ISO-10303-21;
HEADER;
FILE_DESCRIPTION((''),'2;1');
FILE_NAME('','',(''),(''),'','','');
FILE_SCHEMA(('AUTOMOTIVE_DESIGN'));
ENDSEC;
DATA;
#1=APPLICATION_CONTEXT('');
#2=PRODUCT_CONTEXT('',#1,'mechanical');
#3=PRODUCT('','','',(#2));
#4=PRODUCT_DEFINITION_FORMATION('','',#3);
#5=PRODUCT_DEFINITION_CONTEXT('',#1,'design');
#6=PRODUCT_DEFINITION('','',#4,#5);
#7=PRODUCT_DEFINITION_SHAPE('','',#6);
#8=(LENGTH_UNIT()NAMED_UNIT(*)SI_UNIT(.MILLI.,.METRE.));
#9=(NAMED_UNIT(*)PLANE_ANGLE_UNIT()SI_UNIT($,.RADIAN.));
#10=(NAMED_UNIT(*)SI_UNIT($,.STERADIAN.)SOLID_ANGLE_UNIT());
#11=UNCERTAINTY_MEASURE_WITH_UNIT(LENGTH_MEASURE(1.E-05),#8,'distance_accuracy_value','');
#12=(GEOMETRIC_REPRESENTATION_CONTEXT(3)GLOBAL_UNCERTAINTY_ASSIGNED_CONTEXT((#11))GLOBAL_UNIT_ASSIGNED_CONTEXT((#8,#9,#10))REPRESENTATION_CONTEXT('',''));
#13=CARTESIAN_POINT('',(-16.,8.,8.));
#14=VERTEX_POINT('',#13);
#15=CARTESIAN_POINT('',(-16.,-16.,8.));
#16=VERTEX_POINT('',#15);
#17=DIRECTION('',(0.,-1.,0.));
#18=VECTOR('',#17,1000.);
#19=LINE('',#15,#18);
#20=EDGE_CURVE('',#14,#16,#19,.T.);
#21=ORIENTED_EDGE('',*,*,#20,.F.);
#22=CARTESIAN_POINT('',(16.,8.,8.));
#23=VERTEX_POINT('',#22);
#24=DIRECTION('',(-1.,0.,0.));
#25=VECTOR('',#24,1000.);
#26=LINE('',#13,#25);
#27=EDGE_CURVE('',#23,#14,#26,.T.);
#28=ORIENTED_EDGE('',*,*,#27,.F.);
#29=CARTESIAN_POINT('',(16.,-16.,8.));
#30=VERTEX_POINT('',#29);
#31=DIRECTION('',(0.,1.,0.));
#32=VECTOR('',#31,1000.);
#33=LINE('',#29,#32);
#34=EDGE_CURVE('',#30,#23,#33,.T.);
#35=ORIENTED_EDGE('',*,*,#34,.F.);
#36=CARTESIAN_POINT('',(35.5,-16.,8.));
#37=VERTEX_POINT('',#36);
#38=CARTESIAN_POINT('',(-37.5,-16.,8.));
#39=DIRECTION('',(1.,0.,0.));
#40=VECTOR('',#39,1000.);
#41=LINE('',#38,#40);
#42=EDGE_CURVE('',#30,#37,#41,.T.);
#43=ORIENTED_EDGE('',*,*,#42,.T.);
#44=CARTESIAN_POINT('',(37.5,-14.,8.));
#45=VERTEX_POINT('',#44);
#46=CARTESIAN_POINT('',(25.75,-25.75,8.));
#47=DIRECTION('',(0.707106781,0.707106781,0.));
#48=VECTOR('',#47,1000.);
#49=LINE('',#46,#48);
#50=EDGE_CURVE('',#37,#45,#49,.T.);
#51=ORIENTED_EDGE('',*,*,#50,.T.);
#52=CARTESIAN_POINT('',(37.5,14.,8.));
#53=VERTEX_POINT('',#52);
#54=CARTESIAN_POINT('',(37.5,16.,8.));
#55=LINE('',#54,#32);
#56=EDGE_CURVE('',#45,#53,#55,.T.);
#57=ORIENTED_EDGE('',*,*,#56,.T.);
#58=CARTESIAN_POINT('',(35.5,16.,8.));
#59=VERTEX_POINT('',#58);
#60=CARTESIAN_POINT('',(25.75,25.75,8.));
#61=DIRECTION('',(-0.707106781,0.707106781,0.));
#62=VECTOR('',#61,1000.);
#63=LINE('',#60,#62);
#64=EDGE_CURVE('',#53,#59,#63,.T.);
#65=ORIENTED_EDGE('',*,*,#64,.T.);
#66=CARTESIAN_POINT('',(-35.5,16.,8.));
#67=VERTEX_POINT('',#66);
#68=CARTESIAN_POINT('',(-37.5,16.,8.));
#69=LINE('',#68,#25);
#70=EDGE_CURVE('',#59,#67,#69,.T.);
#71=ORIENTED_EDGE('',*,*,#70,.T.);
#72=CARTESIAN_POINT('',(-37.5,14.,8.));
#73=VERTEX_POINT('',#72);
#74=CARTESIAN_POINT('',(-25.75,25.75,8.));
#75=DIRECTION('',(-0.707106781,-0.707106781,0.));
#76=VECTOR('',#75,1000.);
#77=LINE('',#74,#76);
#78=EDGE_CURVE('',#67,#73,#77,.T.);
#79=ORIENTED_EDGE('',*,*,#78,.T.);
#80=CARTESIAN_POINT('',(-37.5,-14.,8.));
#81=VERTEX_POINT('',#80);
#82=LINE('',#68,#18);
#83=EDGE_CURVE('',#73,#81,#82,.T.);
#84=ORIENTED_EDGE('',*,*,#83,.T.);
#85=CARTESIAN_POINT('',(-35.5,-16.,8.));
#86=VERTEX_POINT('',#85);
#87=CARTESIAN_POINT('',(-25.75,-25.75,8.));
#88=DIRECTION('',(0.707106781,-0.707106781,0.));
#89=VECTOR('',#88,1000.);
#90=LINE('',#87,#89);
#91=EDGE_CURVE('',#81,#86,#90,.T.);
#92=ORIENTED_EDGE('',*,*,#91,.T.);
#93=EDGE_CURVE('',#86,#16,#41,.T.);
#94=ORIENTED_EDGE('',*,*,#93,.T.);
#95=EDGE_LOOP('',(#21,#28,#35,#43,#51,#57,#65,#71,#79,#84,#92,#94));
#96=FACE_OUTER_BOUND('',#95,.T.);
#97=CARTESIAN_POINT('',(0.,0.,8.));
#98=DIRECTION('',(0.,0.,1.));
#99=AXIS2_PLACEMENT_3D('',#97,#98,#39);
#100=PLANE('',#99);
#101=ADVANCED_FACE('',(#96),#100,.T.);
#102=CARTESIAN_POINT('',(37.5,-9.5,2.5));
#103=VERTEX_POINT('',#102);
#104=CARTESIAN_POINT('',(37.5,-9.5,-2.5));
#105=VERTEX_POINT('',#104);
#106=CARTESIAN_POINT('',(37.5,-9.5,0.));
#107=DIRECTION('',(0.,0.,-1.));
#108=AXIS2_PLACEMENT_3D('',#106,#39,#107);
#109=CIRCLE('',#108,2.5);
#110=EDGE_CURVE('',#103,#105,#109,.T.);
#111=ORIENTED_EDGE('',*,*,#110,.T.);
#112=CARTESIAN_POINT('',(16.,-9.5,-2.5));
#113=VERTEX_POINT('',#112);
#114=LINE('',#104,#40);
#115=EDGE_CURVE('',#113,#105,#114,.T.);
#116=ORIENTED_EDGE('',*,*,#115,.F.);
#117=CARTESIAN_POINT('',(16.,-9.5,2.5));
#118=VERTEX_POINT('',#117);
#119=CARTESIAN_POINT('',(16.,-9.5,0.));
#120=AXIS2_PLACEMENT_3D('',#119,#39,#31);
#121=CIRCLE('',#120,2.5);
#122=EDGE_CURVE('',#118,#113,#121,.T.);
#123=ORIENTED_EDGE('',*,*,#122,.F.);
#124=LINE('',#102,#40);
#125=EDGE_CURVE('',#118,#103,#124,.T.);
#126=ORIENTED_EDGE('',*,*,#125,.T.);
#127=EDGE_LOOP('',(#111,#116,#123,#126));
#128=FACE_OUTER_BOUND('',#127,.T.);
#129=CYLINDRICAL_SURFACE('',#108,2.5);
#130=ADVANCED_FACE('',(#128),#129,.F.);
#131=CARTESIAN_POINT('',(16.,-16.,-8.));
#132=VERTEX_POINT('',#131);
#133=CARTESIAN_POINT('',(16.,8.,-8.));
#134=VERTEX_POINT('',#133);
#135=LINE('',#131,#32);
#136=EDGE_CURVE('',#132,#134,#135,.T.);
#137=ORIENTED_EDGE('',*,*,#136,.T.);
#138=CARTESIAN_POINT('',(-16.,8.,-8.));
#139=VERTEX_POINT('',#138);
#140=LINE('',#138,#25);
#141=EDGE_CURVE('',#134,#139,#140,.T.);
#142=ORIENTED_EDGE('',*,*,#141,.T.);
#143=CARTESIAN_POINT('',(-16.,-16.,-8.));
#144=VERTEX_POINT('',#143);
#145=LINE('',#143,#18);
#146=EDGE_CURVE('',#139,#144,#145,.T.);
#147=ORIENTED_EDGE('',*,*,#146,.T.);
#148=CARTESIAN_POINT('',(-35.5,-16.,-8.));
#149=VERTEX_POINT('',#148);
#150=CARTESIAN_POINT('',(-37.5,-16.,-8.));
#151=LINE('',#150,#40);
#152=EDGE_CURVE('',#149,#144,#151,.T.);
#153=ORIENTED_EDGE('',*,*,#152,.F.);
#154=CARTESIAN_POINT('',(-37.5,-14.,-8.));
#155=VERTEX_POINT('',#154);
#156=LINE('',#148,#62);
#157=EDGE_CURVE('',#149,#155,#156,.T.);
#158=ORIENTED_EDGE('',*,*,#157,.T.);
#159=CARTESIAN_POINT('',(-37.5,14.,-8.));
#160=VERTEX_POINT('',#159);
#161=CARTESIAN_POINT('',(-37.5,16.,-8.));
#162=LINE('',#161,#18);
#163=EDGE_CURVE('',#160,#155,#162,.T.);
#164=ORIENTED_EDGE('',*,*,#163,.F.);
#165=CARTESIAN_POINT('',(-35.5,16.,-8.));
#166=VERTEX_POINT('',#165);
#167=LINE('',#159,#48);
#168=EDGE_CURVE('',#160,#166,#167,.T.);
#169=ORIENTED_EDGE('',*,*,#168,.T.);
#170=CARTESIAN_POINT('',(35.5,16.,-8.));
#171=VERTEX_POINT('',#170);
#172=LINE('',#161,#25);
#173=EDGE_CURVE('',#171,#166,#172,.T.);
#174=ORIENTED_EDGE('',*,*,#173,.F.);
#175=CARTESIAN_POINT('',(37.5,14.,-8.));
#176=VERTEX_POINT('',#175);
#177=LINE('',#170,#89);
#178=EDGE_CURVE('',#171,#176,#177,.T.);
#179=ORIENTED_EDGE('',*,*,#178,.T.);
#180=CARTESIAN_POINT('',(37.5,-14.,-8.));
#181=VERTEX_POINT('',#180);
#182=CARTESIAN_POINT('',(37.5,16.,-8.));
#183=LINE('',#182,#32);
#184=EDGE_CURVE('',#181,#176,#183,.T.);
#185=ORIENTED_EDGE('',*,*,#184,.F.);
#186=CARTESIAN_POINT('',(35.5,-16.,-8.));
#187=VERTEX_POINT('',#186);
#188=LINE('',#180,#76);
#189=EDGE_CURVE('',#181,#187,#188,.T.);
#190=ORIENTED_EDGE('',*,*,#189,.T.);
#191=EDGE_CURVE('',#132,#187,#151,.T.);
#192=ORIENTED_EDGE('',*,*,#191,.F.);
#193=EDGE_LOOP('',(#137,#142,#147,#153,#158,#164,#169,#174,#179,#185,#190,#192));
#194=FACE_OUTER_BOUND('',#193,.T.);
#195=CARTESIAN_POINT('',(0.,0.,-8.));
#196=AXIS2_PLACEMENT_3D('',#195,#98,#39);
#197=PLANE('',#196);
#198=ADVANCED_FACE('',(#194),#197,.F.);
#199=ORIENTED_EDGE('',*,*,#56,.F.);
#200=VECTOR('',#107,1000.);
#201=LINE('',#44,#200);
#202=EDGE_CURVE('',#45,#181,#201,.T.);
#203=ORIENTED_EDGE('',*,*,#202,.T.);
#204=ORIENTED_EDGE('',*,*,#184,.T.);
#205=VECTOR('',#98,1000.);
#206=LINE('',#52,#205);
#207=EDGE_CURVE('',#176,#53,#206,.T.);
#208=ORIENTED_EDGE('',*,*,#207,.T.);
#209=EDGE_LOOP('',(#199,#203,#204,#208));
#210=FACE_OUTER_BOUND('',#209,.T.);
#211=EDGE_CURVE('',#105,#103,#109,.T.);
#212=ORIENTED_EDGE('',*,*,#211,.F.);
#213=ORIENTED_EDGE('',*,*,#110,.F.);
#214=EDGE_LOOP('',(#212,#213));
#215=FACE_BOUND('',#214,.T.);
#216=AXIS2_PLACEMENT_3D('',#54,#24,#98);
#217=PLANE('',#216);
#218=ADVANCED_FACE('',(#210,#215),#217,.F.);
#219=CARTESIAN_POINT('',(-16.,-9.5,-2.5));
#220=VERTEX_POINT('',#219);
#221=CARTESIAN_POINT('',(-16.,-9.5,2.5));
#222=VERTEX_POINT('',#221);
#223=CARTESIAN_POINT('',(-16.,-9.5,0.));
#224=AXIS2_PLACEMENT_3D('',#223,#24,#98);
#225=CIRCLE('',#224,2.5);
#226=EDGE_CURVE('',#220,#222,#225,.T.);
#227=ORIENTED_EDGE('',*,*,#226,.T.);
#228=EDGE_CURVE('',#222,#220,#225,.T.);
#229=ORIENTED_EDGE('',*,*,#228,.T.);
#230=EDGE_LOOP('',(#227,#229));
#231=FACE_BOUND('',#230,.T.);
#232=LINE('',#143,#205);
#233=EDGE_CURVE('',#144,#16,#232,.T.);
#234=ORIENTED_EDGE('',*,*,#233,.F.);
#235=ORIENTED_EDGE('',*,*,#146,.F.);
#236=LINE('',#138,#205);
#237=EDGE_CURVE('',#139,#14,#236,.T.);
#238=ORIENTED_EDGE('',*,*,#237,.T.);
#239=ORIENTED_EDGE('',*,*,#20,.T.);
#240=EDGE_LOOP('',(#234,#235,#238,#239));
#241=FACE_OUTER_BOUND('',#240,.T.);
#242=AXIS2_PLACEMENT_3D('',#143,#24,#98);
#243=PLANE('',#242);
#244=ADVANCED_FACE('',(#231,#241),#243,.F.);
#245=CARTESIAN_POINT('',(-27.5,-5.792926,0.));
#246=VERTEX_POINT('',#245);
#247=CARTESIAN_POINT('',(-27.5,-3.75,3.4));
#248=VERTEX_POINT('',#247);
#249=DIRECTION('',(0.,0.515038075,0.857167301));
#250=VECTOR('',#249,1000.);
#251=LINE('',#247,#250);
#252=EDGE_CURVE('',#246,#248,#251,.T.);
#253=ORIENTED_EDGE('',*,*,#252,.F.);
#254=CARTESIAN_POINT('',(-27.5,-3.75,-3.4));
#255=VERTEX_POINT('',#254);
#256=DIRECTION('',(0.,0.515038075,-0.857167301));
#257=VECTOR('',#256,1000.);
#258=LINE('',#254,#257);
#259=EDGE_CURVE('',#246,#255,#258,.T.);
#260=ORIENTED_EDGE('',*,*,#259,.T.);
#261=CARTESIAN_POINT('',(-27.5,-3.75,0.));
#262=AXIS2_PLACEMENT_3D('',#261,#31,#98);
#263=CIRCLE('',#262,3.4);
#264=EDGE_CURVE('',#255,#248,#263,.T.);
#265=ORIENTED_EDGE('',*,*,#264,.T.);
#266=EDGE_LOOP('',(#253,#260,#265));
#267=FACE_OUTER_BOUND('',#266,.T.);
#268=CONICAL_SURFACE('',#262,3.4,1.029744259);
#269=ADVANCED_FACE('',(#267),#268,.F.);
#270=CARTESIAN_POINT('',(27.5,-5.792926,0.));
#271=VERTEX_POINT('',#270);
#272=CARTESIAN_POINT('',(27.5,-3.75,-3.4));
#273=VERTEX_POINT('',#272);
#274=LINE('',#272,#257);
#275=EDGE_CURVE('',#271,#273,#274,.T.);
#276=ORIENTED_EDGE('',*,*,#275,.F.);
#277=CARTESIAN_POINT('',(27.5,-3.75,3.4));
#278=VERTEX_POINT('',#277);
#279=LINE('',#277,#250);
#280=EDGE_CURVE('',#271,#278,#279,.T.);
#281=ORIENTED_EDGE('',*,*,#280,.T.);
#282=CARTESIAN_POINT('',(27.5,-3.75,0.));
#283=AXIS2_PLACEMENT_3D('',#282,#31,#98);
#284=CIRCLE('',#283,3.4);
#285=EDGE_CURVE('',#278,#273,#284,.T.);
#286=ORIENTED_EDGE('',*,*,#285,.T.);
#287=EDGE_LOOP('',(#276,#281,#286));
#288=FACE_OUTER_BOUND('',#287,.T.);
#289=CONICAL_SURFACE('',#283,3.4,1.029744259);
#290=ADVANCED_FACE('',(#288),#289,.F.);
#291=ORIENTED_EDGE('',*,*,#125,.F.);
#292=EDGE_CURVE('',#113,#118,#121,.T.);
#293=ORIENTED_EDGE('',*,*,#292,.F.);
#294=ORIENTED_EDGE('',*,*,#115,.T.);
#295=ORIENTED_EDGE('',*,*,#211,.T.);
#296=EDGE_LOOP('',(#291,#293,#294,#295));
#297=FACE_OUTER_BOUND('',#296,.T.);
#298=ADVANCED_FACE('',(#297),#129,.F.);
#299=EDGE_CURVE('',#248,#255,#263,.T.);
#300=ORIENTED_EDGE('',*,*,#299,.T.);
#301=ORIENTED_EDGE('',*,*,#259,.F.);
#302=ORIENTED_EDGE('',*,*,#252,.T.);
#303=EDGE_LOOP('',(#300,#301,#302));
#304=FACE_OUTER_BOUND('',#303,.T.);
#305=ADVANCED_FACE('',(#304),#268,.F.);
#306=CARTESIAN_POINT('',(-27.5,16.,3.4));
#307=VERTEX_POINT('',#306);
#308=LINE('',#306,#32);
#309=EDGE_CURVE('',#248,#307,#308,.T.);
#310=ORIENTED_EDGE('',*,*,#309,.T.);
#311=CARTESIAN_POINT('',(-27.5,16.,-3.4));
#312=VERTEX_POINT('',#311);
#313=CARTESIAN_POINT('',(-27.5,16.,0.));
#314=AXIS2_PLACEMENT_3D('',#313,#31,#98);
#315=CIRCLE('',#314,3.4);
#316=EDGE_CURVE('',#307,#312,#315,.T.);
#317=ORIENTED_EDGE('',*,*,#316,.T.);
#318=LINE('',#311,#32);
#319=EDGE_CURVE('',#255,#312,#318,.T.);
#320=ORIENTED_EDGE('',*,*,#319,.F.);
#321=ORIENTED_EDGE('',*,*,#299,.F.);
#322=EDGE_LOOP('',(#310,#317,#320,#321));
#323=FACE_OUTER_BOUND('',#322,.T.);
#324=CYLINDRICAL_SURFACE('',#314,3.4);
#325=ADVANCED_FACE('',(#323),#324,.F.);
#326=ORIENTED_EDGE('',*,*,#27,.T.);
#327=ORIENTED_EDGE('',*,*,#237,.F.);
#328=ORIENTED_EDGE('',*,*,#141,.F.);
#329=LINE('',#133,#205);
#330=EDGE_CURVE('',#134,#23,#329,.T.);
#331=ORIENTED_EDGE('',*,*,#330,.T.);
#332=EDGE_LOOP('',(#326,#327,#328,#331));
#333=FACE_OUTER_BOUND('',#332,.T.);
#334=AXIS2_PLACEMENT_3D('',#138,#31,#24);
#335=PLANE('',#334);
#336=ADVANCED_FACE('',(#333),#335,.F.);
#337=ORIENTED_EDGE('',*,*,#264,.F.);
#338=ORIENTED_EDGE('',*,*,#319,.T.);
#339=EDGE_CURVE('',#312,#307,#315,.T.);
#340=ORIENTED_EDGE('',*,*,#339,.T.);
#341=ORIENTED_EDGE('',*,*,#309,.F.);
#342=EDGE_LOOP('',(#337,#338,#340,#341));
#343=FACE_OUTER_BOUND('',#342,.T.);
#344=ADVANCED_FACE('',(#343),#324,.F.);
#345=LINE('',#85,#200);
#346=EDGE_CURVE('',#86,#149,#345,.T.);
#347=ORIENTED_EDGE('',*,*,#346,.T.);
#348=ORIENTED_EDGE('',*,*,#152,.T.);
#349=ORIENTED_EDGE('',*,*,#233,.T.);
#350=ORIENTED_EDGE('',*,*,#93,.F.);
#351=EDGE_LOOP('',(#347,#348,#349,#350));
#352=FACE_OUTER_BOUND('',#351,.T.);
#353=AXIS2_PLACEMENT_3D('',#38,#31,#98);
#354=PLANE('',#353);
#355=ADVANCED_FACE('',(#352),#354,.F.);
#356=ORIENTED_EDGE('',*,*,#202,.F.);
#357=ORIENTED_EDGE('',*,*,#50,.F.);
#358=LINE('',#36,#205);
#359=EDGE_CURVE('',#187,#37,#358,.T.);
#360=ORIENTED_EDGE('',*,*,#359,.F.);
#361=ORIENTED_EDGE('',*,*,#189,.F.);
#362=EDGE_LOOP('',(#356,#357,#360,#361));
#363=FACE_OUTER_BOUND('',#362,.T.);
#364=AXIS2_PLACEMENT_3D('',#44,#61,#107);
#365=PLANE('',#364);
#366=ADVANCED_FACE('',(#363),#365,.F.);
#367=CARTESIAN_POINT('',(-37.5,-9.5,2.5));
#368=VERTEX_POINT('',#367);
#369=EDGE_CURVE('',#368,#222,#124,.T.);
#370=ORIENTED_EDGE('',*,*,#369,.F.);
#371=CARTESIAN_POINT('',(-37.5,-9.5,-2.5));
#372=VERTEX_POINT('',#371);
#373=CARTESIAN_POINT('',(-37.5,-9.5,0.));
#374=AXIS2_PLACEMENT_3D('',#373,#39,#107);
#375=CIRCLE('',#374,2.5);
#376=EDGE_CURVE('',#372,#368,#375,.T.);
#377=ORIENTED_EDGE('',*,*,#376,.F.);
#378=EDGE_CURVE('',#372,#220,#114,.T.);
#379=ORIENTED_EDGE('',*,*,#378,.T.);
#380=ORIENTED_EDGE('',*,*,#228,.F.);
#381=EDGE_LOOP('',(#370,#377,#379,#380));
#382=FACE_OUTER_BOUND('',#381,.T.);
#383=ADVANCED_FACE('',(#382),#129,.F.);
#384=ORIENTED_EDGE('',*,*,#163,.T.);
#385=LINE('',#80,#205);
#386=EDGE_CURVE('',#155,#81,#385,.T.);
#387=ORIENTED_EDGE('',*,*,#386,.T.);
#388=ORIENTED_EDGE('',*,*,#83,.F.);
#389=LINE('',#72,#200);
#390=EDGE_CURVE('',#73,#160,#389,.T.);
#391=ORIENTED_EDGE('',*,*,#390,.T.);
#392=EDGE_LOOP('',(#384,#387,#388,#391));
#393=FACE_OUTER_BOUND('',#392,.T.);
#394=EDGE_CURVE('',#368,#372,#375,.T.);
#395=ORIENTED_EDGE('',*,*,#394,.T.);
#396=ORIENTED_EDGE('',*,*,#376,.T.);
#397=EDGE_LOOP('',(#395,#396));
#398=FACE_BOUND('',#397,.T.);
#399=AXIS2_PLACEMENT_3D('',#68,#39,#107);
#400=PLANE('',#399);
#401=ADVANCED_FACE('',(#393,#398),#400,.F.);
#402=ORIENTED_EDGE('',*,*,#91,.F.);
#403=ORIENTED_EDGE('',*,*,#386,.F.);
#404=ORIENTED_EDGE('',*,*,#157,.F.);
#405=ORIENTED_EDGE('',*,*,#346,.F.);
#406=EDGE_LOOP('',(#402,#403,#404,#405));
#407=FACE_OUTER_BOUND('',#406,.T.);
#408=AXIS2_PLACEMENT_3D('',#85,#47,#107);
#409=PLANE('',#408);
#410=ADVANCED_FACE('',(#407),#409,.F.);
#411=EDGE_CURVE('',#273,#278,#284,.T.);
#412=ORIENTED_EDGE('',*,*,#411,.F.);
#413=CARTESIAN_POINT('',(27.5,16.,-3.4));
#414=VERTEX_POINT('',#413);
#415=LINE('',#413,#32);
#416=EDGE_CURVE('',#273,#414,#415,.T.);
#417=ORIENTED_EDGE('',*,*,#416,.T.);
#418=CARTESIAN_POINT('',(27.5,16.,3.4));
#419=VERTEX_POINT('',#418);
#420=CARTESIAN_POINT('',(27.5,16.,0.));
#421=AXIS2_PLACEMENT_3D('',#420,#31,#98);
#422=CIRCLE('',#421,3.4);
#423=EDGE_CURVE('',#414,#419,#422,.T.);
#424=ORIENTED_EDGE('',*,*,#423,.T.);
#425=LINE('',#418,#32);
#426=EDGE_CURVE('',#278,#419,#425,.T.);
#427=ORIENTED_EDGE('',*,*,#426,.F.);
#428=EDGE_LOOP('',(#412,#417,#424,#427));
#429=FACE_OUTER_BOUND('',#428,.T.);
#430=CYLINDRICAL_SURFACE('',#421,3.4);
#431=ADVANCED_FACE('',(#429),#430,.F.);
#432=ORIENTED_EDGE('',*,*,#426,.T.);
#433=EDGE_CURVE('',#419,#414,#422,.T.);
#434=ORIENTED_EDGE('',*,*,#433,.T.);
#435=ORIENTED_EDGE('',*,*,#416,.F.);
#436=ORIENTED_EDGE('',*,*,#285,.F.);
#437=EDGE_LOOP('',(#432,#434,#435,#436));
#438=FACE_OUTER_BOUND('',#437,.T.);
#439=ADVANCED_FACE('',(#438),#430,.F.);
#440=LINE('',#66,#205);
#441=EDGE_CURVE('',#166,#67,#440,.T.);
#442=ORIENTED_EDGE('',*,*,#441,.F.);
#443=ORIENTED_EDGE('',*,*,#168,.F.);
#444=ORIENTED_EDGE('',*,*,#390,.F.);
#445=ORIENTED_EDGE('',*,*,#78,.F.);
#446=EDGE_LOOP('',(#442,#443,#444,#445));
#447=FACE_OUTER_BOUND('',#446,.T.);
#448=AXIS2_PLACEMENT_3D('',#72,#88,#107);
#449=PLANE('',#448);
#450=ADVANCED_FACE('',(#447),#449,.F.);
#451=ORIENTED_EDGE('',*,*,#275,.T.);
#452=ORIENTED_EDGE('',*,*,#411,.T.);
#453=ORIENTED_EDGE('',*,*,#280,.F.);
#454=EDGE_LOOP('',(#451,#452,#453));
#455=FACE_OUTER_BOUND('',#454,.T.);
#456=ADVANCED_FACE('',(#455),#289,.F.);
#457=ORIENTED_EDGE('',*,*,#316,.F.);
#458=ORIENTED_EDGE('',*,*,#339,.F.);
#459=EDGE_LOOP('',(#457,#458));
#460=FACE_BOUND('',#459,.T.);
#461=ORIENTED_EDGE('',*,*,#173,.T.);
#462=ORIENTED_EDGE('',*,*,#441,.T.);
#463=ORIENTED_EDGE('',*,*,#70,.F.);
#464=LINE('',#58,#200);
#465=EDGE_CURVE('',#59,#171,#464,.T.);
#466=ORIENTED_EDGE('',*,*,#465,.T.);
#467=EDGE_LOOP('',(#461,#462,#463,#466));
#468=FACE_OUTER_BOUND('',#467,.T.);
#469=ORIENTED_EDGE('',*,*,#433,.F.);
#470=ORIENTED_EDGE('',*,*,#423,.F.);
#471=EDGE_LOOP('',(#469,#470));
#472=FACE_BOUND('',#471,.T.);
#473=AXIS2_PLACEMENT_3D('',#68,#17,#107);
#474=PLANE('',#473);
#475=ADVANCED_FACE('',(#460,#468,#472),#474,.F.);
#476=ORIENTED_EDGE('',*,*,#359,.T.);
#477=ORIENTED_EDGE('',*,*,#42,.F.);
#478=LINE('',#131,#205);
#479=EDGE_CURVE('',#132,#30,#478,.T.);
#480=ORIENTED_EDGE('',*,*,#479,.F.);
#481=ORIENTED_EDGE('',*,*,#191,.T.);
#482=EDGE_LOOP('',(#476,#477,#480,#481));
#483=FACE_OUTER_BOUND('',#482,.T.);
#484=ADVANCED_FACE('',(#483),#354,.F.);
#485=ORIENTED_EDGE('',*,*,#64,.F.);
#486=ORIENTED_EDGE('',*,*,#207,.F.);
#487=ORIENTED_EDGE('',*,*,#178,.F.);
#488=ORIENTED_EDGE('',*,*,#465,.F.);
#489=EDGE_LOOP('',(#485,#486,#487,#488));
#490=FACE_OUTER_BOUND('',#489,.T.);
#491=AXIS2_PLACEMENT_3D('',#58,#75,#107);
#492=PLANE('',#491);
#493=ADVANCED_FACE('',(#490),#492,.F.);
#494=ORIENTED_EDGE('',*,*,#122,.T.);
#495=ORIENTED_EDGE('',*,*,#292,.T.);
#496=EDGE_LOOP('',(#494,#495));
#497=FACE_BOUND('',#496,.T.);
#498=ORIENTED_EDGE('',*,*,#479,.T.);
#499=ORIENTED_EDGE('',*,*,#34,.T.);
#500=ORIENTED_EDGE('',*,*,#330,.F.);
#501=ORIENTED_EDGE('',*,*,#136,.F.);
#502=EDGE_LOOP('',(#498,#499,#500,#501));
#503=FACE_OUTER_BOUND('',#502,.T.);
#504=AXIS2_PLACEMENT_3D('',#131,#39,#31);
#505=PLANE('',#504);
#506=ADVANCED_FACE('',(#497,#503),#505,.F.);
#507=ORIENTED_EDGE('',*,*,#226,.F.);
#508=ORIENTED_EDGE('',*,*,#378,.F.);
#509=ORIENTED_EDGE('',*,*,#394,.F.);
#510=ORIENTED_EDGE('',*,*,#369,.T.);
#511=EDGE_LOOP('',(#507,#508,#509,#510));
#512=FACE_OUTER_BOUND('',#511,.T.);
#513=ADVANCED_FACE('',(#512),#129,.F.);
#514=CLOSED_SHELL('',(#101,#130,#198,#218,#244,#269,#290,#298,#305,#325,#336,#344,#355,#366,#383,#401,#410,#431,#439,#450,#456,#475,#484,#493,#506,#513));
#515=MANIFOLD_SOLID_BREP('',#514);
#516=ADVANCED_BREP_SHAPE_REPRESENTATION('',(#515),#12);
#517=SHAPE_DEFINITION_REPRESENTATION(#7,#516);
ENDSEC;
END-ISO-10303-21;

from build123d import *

# Parameters (mm, degrees)
SKETCH_1_W             = 75
SKETCH_1_H             = 32
EXTRUDE_1_DEPTH        = 8
SKETCH_3_W             = 32
SKETCH_3_H             = 24
CUT_EXTRUDE_1_DEPTH    = 44.797830997
HOLE_WIZARD_M6_1_D     = 5
CHAMFER_1_SIZE         = 2
HOLE_WIZARD_M8_1_D     = 6.8
HOLE_WIZARD_M8_1_DEPTH = 19.75
HOLE_WIZARD_M8_1_TIP   = 2.042926105
CHAMFER_2_SIZE         = 2


with BuildPart() as part:
    # 草图1 → 凸台-拉伸1 (new, symmetric)
    with BuildSketch(Plane.XY):
        Rectangle(SKETCH_1_W, SKETCH_1_H)
    extrude(amount=EXTRUDE_1_DEPTH, both=True)

    # 草图3 → 切除-拉伸1 (cut, through all)
    with BuildSketch(Plane.XY.offset(8)):
        with Locations((0, -4)):
            Rectangle(SKETCH_3_W, SKETCH_3_H)
    extrude(amount=-CUT_EXTRUDE_1_DEPTH, mode=Mode.SUBTRACT)

    # M6 螺纹孔1 (through all)
    with Locations(Plane(origin=(37.5, 0, 0), x_dir=(0, 0, -1), z_dir=(1, 0, 0))):
        with Locations((0, -9.5)):
            Hole(HOLE_WIZARD_M6_1_D / 2)

    # 倒角1
    chamfer_1_edges = [part.edges().sort_by_distance(p)[0] for p in [
        (-37.5, 16, 0),
        (37.5, 16, 0),
    ]]
    chamfer(chamfer_1_edges, length=CHAMFER_1_SIZE)

    # M8 螺纹孔1
    with Locations(Plane(origin=(0, 16, 0), x_dir=(1, 0, 0), z_dir=(0, 1, 0))):
        with Locations((-27.5, 0), (27.5, 0)):
            Hole(HOLE_WIZARD_M8_1_D / 2, depth=HOLE_WIZARD_M8_1_DEPTH)
            with Locations((0, 0, -(HOLE_WIZARD_M8_1_DEPTH + HOLE_WIZARD_M8_1_TIP / 2))):  # 118° drill point
                Cone(0, HOLE_WIZARD_M8_1_D / 2, HOLE_WIZARD_M8_1_TIP, mode=Mode.SUBTRACT)

    # 倒角2
    chamfer_2_edges = [part.edges().sort_by_distance(p)[0] for p in [
        (37.5, -16, 0),
        (-37.5, -16, 0),
    ]]
    chamfer(chamfer_2_edges, length=CHAMFER_2_SIZE)


solid = part.part
